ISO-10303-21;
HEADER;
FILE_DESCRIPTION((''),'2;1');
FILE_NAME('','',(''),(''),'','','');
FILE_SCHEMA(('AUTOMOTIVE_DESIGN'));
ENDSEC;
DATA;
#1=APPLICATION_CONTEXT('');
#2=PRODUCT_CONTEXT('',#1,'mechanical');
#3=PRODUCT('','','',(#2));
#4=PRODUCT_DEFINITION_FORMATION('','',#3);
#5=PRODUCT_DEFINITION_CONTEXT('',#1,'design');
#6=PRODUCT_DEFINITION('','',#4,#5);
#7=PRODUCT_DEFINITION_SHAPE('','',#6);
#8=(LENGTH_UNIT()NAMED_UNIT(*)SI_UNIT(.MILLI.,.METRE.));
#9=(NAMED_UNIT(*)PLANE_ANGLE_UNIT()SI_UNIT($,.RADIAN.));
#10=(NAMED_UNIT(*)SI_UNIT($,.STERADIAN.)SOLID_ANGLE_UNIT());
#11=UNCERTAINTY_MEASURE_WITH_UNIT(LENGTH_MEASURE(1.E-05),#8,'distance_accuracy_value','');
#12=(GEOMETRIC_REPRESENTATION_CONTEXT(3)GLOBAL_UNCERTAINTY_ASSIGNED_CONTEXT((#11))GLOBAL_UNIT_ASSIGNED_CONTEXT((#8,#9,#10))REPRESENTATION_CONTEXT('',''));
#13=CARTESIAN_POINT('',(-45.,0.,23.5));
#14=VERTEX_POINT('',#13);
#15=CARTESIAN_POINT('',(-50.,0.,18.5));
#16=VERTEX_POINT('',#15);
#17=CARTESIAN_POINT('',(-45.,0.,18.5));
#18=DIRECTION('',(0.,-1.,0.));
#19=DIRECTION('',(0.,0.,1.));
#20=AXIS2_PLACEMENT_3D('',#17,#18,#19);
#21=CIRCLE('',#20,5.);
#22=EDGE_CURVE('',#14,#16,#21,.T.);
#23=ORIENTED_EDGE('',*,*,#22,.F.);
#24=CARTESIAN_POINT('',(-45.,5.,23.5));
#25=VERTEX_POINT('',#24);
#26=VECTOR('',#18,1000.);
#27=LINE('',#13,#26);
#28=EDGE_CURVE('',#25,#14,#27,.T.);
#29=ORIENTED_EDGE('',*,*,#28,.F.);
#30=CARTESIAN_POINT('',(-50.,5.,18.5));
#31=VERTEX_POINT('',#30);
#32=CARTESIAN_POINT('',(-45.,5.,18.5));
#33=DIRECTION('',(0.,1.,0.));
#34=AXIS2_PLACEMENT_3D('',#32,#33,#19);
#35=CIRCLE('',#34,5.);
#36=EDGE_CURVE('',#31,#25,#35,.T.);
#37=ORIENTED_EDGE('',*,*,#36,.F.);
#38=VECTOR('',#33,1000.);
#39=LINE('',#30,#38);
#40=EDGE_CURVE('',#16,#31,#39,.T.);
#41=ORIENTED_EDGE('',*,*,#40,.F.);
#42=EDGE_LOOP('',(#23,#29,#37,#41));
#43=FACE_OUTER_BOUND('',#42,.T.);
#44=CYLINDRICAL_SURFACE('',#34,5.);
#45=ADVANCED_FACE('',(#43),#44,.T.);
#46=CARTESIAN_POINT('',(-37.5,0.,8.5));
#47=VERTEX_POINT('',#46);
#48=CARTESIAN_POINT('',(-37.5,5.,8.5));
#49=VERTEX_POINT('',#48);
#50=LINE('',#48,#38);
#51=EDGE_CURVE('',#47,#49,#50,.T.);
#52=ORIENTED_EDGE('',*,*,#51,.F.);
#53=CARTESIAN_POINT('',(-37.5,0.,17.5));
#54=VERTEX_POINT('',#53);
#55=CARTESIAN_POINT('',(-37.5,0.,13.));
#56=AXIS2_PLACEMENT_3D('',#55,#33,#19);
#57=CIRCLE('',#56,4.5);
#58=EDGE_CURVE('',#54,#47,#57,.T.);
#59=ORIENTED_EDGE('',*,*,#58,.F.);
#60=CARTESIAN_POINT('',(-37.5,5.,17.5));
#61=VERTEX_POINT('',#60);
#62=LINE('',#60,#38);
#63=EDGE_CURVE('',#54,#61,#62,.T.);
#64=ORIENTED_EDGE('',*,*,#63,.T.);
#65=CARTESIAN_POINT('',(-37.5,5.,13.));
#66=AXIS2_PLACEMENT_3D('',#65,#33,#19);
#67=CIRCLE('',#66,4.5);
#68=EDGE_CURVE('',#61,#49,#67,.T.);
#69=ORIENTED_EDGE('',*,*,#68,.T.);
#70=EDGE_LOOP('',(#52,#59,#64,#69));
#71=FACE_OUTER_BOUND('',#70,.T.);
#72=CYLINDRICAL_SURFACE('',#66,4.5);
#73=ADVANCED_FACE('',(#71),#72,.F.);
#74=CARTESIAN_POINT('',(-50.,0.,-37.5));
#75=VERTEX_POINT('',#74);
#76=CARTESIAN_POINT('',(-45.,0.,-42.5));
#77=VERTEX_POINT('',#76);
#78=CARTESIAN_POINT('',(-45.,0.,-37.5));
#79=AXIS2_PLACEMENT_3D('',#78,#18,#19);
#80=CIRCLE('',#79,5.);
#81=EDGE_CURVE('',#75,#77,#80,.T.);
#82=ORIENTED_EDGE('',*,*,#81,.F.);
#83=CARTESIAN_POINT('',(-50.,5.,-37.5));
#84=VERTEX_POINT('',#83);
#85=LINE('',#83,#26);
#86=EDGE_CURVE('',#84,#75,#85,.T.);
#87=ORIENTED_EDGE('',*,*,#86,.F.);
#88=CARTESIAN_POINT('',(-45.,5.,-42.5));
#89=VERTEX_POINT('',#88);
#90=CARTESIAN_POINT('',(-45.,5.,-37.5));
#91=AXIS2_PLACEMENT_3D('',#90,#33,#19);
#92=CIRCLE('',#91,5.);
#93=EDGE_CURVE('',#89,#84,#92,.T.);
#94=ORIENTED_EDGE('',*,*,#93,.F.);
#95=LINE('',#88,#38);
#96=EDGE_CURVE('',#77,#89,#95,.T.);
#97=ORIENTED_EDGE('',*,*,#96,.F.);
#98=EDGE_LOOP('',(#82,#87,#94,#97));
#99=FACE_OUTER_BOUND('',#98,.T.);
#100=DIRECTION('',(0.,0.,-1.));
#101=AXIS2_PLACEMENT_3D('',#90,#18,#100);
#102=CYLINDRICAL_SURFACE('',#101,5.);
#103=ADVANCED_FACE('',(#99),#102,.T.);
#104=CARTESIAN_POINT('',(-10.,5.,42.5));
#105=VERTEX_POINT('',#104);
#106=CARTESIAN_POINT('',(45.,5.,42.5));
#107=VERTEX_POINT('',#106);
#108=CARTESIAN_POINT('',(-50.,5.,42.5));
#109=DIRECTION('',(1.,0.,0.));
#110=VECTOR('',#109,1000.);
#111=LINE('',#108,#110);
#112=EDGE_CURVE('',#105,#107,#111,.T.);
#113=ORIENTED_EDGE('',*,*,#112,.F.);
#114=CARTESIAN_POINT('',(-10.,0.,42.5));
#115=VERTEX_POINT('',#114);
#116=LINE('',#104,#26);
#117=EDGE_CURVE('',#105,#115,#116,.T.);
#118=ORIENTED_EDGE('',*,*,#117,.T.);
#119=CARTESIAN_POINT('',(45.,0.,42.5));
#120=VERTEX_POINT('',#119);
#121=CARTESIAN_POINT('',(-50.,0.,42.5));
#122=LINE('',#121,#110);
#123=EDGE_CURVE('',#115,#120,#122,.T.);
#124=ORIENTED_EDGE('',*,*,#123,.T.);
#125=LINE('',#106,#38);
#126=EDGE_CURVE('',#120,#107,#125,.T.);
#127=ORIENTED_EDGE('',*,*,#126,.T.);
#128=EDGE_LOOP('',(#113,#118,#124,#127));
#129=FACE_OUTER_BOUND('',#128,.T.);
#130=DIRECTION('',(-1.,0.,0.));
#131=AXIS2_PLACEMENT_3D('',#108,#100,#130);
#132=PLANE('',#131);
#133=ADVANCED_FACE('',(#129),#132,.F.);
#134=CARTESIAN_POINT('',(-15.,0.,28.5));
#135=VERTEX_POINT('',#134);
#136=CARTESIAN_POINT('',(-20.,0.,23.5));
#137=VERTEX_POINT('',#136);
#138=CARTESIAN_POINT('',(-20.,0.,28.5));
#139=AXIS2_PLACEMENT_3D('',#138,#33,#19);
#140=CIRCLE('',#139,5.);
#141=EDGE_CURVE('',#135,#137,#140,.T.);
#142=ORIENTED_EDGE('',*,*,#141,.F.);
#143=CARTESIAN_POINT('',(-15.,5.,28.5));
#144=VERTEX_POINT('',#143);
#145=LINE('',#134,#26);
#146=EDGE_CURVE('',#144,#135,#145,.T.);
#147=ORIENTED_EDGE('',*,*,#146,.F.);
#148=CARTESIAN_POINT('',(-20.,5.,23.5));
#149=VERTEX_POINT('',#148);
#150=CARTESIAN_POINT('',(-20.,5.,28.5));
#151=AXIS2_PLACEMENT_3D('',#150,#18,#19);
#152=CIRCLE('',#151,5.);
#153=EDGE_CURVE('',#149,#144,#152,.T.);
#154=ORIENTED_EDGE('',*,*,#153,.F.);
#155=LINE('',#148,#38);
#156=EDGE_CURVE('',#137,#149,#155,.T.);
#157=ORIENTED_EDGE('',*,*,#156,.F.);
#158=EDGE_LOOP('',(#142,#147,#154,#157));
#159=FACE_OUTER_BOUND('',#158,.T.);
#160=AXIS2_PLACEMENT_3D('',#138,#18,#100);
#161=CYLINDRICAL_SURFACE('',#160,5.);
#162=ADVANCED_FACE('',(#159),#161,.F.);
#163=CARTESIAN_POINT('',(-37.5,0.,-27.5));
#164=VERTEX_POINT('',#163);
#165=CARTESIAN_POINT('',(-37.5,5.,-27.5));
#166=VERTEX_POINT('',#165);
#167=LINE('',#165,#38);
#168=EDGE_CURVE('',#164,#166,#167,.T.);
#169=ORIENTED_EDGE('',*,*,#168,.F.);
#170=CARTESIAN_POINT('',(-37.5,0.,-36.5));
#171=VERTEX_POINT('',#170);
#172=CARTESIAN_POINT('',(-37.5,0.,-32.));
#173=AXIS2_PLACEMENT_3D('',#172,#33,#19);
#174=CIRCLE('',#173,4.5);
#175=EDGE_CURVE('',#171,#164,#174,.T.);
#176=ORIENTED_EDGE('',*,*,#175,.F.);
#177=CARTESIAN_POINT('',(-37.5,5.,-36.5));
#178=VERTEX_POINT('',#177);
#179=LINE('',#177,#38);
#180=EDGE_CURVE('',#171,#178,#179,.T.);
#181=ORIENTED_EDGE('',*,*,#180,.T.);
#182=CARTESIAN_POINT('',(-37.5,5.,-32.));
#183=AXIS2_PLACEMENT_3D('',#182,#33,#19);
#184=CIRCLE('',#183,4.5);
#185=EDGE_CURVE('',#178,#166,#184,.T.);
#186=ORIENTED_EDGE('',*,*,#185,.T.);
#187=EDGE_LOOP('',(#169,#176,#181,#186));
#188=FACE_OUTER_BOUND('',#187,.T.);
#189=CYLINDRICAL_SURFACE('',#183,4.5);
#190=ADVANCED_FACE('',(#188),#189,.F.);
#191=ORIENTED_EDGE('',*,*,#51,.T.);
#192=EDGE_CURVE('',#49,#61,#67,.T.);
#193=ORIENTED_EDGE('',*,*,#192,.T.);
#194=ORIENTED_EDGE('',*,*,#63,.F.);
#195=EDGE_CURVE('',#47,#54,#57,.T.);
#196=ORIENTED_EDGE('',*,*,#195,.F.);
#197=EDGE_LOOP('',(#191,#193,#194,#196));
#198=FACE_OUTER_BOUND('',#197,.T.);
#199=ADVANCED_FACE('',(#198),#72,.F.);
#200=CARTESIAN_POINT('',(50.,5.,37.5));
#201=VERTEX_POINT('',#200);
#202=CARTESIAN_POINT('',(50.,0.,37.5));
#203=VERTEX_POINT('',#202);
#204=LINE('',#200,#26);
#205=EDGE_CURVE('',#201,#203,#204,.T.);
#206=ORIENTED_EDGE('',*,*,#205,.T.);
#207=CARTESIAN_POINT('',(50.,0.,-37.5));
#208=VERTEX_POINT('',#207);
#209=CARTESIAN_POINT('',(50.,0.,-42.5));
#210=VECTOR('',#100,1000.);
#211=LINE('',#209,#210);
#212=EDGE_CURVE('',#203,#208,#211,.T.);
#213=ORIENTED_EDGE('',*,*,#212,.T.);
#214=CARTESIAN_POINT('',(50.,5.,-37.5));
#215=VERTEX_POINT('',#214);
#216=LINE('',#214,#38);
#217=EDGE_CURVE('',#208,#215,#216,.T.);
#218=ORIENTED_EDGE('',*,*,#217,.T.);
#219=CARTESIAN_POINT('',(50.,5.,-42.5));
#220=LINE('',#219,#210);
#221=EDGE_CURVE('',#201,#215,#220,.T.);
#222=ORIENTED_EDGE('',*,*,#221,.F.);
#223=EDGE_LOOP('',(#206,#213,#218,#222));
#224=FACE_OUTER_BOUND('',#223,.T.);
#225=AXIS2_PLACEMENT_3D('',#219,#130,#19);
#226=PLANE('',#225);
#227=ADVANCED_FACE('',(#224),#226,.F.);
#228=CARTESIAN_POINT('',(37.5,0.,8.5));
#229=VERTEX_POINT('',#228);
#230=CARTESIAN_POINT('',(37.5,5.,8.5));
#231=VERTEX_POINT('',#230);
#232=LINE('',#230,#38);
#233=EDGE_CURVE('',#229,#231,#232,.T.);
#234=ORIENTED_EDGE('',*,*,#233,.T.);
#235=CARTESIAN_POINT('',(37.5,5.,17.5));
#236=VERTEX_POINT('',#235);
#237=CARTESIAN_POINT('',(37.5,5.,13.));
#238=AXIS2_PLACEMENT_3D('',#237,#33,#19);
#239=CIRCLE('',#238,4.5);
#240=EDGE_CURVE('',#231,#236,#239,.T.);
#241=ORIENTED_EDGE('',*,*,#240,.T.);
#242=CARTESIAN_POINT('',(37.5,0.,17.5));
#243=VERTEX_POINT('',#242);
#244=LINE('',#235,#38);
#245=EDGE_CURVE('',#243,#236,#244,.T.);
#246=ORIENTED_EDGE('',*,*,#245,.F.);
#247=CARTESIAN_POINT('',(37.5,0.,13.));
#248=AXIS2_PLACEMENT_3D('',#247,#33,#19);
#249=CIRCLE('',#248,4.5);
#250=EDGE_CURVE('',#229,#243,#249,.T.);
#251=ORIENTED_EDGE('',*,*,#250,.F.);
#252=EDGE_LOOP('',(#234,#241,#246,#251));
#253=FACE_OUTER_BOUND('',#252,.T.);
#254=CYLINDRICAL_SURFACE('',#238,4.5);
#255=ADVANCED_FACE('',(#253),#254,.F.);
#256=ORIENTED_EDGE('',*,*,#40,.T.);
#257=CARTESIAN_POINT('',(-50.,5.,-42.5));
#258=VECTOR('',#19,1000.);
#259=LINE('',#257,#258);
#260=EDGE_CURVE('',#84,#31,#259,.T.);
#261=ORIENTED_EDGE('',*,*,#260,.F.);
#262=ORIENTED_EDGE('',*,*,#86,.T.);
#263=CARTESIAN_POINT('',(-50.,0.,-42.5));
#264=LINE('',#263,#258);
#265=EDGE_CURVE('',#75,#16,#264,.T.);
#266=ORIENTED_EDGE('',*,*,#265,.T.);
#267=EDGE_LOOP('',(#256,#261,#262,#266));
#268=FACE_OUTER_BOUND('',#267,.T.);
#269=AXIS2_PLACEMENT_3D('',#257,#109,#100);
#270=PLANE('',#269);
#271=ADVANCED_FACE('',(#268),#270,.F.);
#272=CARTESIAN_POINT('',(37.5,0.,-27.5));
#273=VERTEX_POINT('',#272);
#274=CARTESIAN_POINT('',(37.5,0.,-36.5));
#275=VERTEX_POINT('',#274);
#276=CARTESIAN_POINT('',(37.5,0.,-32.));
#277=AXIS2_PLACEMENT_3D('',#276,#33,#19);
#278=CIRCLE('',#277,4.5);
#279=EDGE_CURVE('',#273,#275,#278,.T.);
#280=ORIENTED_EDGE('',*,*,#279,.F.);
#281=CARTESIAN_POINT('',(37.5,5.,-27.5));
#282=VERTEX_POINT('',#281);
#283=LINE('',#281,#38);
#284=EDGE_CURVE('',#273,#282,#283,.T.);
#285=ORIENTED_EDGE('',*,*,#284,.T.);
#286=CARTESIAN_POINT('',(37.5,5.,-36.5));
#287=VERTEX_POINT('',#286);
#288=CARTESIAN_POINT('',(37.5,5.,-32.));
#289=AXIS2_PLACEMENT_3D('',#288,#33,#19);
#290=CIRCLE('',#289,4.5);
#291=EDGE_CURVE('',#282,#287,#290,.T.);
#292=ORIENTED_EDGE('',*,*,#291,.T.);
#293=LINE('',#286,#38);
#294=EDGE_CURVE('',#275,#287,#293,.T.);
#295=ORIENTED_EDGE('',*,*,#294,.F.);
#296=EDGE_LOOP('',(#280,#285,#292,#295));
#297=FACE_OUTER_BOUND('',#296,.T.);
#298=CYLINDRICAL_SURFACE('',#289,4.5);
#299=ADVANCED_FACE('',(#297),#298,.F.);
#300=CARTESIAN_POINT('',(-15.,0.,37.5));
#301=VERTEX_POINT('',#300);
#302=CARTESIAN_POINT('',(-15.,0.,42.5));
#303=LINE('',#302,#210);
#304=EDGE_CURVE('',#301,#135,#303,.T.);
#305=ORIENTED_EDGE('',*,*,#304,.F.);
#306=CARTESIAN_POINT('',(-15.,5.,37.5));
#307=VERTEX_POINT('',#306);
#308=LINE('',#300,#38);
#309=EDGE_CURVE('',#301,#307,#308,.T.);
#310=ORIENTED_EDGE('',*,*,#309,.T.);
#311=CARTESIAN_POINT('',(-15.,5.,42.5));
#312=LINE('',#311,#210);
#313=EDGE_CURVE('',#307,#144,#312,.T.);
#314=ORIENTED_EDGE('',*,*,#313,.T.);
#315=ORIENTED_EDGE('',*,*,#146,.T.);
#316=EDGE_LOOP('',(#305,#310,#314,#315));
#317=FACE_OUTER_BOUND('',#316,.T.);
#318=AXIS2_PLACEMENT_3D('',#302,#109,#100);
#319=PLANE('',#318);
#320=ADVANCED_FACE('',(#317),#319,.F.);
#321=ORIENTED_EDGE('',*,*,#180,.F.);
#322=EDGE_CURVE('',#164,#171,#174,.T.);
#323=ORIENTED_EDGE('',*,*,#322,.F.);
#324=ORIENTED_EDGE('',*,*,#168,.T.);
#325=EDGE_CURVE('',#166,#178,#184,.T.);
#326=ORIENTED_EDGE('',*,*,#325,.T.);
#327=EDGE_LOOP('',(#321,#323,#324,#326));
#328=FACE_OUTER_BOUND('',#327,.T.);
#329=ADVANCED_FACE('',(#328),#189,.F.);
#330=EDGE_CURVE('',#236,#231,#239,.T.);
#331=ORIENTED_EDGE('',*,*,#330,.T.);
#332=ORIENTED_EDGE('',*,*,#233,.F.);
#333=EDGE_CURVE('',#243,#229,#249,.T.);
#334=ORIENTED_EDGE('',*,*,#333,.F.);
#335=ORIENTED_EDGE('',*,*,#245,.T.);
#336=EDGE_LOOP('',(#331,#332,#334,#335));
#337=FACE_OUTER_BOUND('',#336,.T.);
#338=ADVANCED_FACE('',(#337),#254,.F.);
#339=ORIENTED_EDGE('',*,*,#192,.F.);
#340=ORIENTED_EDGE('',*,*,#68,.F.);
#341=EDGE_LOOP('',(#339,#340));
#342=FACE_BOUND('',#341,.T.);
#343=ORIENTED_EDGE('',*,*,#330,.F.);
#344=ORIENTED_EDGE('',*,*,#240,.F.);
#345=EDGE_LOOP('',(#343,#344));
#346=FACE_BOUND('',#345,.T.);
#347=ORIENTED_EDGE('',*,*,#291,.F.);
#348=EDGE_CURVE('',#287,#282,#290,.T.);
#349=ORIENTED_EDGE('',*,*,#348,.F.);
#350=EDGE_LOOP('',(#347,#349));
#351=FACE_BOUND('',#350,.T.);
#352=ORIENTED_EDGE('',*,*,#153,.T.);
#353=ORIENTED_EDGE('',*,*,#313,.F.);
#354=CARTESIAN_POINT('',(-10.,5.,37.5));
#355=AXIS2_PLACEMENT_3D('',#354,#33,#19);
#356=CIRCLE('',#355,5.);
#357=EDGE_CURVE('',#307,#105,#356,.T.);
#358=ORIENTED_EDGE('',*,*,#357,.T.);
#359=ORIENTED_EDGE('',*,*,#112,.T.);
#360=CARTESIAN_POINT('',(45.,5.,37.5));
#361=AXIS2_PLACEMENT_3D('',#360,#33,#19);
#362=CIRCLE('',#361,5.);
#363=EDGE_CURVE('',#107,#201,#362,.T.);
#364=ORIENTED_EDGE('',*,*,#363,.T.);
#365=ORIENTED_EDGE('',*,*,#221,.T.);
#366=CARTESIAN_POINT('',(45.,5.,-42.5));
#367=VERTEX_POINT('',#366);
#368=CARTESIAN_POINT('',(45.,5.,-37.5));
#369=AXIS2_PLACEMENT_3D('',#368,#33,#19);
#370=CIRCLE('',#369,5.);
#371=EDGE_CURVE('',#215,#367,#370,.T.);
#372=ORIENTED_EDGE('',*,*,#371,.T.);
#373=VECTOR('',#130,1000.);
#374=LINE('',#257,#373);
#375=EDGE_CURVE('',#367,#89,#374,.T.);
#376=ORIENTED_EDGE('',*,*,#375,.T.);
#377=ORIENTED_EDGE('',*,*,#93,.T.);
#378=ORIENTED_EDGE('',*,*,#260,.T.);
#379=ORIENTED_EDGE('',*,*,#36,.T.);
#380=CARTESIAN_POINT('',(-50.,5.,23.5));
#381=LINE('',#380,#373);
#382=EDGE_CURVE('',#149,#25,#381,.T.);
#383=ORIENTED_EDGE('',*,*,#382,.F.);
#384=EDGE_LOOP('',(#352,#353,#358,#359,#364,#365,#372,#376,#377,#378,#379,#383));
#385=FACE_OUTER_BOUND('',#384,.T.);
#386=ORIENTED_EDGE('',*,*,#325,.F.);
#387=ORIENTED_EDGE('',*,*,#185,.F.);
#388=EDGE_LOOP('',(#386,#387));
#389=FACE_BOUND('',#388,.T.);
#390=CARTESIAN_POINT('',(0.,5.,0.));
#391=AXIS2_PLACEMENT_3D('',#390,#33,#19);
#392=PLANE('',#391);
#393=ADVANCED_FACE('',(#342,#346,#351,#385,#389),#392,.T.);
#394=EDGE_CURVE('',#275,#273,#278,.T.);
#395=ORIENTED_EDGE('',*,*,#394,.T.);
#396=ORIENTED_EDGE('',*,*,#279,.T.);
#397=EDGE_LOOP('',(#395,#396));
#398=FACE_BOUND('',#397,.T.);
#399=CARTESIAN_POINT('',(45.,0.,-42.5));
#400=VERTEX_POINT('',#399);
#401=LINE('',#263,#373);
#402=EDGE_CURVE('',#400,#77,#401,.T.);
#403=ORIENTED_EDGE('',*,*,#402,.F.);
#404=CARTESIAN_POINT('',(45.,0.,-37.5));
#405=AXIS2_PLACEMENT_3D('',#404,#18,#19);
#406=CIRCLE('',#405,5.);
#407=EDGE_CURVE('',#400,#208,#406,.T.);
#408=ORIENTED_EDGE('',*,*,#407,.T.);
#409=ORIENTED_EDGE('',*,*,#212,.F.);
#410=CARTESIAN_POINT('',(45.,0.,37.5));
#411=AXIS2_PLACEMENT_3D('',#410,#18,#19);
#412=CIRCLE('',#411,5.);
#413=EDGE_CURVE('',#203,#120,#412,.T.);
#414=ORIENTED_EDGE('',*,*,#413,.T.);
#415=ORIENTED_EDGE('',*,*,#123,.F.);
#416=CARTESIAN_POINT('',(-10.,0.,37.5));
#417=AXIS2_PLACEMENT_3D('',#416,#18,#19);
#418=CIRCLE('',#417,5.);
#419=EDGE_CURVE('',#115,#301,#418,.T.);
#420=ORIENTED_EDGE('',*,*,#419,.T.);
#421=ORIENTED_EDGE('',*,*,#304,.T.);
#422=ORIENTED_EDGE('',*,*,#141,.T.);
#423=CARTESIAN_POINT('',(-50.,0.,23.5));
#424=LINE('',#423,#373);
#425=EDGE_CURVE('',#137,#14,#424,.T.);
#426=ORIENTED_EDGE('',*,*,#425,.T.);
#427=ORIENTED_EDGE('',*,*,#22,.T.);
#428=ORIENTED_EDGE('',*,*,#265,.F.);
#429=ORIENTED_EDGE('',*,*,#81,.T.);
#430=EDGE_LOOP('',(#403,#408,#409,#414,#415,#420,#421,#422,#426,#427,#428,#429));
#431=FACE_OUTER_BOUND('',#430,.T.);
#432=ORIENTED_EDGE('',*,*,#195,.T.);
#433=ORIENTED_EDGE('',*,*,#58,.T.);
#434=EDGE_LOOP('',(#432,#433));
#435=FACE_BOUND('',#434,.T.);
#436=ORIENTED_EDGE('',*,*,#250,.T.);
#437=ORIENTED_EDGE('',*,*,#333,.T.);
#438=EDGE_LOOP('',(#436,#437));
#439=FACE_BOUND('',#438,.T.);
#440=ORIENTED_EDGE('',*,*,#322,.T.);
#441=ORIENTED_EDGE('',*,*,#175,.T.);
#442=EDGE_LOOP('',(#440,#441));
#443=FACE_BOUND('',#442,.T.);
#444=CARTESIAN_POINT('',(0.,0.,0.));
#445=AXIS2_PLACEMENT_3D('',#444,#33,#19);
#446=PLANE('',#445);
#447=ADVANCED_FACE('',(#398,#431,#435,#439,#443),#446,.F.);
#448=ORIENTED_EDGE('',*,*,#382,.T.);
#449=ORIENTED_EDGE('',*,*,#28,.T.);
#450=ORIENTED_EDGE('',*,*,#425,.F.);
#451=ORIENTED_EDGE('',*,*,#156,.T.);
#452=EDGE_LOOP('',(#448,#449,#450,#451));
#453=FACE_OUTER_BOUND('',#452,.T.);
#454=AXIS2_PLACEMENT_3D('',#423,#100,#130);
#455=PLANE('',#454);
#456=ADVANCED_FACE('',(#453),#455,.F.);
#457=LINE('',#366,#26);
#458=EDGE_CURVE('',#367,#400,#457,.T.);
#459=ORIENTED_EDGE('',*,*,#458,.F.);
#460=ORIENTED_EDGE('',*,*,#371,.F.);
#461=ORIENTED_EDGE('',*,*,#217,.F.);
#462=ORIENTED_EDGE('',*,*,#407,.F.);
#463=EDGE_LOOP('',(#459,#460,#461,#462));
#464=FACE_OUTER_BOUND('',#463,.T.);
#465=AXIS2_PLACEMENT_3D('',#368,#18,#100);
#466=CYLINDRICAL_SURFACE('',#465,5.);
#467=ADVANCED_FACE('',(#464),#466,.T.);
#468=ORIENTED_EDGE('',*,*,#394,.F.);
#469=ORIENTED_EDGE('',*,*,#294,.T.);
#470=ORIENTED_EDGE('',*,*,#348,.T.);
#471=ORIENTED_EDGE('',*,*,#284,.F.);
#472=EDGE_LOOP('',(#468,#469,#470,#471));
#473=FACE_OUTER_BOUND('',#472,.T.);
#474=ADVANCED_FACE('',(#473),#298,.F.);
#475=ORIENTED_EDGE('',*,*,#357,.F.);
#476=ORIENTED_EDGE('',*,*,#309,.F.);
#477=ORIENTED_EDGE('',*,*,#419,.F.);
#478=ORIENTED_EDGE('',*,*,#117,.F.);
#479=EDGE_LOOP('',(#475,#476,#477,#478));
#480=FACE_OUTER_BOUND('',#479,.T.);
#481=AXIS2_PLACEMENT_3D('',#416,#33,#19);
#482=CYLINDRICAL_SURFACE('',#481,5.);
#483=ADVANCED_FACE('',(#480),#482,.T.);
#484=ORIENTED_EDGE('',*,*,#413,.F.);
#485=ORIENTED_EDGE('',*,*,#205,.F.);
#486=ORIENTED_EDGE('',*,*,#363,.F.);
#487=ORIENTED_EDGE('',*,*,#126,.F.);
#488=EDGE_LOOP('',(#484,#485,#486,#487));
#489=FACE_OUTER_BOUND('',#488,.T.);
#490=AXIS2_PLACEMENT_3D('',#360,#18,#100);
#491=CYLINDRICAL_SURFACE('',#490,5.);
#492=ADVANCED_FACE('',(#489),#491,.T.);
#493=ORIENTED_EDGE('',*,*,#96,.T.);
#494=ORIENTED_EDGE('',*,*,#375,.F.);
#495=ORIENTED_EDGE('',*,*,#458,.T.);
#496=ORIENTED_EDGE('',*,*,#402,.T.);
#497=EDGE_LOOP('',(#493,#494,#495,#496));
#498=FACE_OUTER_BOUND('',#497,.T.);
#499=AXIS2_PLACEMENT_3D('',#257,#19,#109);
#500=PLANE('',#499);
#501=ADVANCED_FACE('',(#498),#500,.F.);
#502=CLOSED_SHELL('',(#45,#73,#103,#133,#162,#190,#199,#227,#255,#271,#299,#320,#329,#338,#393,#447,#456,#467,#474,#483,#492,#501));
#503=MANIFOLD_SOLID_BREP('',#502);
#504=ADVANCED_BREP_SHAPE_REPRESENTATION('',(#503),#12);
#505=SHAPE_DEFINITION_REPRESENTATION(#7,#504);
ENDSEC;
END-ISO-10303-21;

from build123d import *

# Parameters (mm, degrees)
SKETCH2_W            = 100
SKETCH2_H            = 85
BOSS_EXTRUDE1_DEPTH  = 5
M8_CLEARANCE_HOLE1_D = 9
FILLET1_R            = 5
SKETCH7_W            = 35
SKETCH7_H            = 19
CUT_EXTRUDE1_DEPTH   = 5
FILLET2_R            = 5


with BuildPart() as part:
    # Sketch2 → Boss-Extrude1 (new body)
    with BuildSketch(Plane(origin=(0, 0, 0), x_dir=(1, 0, 0), z_dir=(0, 1, 0))):
        Rectangle(SKETCH2_W, SKETCH2_H)
    extrude(amount=BOSS_EXTRUDE1_DEPTH)

    # M8 Clearance Hole1 (through all)
    with Locations(Plane(origin=(0, 5, 0), x_dir=(1, 0, 0), z_dir=(0, 1, 0))):
        with Locations((-37.5, 32), (37.5, 32), (37.5, -13), (-37.5, -13)):
            Hole(M8_CLEARANCE_HOLE1_D / 2)

    # Fillet1
    fillet1_edges = [part.edges().sort_by_distance(p)[0] for p in [
        (50, 2.5, 42.5),
        (-50, 2.5, -42.5),
        (50, 2.5, -42.5),
    ]]
    fillet(fillet1_edges, radius=FILLET1_R)

    # Sketch7 → Cut-Extrude1 (cut)
    with BuildSketch(Plane(origin=(0, 5, 0), x_dir=(1, 0, 0), z_dir=(0, 1, 0))):
        with Locations((-32.5, -33)):
            Rectangle(SKETCH7_W, SKETCH7_H)
    extrude(amount=-CUT_EXTRUDE1_DEPTH, mode=Mode.SUBTRACT)

    # Fillet2
    fillet2_edges = [part.edges().sort_by_distance(p)[0] for p in [
        (-50, 2.5, 23.5),
        (-15, 2.5, 23.5),
        (-15, 2.5, 42.5),
    ]]
    fillet(fillet2_edges, radius=FILLET2_R)


solid = part.part
